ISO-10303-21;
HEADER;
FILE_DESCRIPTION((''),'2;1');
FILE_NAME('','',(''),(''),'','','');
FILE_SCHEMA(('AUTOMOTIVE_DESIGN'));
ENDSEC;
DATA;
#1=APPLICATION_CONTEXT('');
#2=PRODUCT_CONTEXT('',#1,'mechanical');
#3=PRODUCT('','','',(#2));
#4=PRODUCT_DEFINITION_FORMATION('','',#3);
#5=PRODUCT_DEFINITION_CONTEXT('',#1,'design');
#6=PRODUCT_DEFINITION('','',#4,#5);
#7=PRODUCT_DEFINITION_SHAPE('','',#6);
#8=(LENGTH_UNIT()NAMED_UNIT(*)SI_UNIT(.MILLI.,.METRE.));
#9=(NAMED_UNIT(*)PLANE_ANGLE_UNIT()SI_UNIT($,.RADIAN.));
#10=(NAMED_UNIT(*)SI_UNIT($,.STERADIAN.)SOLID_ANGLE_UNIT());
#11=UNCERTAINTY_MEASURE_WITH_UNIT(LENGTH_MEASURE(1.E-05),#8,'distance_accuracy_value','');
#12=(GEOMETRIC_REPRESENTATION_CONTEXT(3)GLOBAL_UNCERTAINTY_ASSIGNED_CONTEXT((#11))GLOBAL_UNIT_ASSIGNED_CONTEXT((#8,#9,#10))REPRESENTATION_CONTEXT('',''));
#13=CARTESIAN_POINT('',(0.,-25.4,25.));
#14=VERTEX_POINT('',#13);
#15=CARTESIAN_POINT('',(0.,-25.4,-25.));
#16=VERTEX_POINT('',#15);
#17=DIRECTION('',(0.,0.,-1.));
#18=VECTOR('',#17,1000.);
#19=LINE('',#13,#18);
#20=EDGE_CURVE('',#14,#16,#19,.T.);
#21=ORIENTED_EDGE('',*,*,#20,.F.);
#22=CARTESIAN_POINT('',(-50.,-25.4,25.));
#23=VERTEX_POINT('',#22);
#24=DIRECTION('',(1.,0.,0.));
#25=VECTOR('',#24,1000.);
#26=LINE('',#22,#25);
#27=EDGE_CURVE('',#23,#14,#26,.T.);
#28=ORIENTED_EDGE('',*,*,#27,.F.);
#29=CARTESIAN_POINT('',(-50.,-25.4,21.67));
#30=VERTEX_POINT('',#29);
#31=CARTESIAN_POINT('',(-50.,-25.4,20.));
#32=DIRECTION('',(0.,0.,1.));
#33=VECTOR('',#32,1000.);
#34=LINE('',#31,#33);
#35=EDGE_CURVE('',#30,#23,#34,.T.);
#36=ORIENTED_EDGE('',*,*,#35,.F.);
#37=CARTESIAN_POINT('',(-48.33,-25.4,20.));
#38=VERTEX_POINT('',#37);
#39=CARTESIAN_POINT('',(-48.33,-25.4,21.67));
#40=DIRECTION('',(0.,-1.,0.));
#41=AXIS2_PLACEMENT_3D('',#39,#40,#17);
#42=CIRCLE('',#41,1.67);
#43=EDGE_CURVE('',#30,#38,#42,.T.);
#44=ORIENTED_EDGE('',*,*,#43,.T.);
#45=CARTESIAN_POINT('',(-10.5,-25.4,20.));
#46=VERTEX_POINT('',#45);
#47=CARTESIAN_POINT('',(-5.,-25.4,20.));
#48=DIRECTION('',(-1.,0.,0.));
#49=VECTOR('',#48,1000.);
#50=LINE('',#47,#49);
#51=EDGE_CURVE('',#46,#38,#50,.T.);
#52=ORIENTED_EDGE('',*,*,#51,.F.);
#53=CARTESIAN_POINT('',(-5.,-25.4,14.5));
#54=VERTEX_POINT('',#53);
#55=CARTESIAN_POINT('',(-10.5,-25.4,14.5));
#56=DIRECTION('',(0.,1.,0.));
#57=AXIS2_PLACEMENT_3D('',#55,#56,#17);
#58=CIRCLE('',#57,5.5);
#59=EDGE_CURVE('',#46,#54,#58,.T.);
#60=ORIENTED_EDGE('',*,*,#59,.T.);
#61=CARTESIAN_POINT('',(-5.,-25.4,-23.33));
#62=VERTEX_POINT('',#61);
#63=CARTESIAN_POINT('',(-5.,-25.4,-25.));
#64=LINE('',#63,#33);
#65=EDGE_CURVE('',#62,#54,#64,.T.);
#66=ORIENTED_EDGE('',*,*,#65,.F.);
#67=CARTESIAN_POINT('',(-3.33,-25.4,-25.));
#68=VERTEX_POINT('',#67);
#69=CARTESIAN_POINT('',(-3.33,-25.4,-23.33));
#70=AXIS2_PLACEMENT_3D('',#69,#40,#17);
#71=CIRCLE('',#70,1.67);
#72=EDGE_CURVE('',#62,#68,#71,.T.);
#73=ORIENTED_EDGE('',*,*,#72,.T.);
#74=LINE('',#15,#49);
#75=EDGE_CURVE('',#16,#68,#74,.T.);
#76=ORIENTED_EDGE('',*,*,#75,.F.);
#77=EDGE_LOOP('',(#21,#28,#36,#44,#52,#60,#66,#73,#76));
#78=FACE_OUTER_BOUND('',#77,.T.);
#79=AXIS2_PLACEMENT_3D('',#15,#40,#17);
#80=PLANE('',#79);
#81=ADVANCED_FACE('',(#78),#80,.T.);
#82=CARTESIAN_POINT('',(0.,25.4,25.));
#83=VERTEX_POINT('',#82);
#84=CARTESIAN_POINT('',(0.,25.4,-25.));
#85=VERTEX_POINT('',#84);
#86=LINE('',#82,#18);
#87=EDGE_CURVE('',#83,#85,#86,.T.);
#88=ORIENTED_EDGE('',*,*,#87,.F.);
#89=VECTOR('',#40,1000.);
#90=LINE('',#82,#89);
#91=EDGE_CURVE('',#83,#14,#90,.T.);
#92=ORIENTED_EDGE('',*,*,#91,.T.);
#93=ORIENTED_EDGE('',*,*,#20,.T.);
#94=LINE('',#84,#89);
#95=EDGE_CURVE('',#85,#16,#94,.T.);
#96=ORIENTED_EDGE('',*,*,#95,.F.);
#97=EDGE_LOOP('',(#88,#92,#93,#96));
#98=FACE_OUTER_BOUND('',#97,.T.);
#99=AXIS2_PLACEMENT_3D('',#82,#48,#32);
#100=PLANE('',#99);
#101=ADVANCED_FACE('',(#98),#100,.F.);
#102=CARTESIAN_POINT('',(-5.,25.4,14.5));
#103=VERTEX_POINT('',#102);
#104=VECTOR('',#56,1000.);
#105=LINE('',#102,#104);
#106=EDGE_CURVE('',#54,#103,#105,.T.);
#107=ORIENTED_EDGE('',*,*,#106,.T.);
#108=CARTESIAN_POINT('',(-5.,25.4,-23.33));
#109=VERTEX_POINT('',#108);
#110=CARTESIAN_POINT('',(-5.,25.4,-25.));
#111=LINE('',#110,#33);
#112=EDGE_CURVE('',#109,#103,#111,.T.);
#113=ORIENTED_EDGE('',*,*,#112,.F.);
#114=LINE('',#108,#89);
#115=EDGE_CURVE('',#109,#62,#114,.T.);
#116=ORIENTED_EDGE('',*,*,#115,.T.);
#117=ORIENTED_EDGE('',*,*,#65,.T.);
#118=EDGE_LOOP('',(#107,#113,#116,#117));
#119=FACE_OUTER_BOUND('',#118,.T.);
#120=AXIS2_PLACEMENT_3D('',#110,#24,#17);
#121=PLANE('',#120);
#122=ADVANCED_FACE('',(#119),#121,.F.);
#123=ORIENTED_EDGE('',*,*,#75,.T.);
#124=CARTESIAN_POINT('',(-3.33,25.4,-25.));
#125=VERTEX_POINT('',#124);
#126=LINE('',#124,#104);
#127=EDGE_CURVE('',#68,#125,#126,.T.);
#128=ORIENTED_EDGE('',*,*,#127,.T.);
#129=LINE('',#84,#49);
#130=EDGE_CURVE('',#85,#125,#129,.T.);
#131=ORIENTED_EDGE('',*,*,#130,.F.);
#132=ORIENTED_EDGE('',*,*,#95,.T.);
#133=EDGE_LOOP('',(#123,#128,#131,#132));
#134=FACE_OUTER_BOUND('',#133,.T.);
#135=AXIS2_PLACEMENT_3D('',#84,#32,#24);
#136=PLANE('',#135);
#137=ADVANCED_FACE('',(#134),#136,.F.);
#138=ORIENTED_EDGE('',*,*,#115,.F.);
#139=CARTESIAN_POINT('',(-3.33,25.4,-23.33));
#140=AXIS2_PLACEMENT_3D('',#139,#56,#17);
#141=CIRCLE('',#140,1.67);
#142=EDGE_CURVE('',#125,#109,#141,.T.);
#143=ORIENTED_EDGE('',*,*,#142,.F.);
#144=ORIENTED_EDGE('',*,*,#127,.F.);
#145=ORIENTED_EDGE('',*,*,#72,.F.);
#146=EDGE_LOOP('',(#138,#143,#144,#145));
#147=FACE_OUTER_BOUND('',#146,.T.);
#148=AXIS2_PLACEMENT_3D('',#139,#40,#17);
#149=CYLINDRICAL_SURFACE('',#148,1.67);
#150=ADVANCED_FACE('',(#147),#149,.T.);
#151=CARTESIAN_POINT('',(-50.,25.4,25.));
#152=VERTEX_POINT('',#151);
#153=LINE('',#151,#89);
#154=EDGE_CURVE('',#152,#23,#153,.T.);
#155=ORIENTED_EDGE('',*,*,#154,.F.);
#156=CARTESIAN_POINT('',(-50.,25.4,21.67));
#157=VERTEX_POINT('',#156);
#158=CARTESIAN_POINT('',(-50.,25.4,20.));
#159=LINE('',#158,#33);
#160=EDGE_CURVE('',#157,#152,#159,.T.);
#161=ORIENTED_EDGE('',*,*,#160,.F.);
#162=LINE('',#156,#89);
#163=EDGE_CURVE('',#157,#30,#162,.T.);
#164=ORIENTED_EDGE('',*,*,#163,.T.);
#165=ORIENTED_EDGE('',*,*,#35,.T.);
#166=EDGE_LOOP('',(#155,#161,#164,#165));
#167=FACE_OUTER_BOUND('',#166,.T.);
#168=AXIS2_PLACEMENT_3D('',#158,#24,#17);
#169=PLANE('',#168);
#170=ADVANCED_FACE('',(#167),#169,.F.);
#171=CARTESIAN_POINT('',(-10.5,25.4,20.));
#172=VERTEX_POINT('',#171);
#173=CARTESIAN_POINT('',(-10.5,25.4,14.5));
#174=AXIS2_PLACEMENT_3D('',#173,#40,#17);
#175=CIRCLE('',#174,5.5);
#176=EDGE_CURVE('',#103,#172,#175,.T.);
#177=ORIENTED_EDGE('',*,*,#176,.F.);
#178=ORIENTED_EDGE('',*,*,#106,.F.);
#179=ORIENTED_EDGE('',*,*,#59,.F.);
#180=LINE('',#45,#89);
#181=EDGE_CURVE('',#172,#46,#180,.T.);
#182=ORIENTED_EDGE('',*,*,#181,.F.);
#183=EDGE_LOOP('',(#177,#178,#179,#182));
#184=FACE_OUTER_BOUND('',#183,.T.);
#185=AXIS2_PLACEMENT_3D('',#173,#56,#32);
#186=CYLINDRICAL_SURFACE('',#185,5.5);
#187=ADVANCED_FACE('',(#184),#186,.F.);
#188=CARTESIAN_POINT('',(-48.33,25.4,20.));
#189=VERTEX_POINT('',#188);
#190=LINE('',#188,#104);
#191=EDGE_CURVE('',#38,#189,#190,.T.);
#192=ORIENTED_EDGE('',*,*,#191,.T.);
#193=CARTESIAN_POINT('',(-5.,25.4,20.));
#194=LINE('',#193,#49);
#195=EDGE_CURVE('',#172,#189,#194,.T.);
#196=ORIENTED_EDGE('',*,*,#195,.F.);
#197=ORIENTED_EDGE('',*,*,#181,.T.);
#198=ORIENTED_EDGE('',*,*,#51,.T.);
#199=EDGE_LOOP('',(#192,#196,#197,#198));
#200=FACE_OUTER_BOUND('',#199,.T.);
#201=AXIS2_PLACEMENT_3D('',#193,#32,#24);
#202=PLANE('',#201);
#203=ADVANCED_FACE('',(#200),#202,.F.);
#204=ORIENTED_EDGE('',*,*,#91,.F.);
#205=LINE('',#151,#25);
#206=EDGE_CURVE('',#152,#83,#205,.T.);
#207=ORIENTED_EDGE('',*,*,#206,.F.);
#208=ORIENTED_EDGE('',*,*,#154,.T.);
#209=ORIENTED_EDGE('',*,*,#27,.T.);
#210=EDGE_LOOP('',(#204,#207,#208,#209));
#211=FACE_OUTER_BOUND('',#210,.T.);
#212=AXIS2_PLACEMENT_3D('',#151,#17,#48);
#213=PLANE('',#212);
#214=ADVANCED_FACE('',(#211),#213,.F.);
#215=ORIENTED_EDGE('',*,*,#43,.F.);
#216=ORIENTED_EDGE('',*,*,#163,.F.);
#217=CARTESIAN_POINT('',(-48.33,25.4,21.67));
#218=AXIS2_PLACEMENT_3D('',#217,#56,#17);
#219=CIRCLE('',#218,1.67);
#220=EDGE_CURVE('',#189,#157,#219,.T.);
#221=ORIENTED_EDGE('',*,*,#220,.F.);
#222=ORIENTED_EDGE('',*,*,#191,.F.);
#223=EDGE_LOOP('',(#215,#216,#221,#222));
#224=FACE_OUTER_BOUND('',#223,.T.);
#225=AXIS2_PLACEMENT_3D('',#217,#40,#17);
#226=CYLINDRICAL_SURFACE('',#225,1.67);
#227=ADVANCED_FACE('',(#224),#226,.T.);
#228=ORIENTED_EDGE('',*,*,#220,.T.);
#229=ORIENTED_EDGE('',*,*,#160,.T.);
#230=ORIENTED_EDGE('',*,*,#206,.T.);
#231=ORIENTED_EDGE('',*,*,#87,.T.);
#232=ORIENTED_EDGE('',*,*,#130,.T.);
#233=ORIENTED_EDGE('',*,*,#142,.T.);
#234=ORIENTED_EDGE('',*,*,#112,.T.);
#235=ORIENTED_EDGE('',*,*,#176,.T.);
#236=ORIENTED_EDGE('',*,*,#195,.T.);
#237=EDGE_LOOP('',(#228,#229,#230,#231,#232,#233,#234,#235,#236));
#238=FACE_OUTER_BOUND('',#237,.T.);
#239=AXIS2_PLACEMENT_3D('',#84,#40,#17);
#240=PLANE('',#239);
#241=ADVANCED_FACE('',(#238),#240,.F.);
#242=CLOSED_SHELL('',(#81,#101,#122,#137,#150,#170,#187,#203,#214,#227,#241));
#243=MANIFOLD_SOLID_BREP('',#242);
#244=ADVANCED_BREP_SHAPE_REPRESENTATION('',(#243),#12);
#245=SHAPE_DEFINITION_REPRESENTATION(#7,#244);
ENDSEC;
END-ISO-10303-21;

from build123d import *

# Parameters (mm, degrees)
EXTRUDE1_DEPTH = 25.4
FILLET1_R      = 5.5
FILLET2_R      = 1.67


with BuildPart() as part:
    # Sketch1 → Extrude1 (new, symmetric)
    with BuildSketch(Plane(origin=(0, 0, 0), x_dir=(1, 0, 0), z_dir=(0, 1, 0))):
        Polygon((0, -25), (0, 25), (-5, 25), (-5, -20), (-50, -20), (-50, -25), align=None)
    extrude(amount=EXTRUDE1_DEPTH, both=True)

    # Fillet1
    fillet1_edges = [part.edges().sort_by_distance(p)[0] for p in [
        (-5, 0, 20),
    ]]
    fillet(fillet1_edges, radius=FILLET1_R)

    # Fillet2
    fillet2_edges = [part.edges().sort_by_distance(p)[0] for p in [
        (-50, 0, 20),
        (-5, 0, -25),
    ]]
    fillet(fillet2_edges, radius=FILLET2_R)


solid = part.part
